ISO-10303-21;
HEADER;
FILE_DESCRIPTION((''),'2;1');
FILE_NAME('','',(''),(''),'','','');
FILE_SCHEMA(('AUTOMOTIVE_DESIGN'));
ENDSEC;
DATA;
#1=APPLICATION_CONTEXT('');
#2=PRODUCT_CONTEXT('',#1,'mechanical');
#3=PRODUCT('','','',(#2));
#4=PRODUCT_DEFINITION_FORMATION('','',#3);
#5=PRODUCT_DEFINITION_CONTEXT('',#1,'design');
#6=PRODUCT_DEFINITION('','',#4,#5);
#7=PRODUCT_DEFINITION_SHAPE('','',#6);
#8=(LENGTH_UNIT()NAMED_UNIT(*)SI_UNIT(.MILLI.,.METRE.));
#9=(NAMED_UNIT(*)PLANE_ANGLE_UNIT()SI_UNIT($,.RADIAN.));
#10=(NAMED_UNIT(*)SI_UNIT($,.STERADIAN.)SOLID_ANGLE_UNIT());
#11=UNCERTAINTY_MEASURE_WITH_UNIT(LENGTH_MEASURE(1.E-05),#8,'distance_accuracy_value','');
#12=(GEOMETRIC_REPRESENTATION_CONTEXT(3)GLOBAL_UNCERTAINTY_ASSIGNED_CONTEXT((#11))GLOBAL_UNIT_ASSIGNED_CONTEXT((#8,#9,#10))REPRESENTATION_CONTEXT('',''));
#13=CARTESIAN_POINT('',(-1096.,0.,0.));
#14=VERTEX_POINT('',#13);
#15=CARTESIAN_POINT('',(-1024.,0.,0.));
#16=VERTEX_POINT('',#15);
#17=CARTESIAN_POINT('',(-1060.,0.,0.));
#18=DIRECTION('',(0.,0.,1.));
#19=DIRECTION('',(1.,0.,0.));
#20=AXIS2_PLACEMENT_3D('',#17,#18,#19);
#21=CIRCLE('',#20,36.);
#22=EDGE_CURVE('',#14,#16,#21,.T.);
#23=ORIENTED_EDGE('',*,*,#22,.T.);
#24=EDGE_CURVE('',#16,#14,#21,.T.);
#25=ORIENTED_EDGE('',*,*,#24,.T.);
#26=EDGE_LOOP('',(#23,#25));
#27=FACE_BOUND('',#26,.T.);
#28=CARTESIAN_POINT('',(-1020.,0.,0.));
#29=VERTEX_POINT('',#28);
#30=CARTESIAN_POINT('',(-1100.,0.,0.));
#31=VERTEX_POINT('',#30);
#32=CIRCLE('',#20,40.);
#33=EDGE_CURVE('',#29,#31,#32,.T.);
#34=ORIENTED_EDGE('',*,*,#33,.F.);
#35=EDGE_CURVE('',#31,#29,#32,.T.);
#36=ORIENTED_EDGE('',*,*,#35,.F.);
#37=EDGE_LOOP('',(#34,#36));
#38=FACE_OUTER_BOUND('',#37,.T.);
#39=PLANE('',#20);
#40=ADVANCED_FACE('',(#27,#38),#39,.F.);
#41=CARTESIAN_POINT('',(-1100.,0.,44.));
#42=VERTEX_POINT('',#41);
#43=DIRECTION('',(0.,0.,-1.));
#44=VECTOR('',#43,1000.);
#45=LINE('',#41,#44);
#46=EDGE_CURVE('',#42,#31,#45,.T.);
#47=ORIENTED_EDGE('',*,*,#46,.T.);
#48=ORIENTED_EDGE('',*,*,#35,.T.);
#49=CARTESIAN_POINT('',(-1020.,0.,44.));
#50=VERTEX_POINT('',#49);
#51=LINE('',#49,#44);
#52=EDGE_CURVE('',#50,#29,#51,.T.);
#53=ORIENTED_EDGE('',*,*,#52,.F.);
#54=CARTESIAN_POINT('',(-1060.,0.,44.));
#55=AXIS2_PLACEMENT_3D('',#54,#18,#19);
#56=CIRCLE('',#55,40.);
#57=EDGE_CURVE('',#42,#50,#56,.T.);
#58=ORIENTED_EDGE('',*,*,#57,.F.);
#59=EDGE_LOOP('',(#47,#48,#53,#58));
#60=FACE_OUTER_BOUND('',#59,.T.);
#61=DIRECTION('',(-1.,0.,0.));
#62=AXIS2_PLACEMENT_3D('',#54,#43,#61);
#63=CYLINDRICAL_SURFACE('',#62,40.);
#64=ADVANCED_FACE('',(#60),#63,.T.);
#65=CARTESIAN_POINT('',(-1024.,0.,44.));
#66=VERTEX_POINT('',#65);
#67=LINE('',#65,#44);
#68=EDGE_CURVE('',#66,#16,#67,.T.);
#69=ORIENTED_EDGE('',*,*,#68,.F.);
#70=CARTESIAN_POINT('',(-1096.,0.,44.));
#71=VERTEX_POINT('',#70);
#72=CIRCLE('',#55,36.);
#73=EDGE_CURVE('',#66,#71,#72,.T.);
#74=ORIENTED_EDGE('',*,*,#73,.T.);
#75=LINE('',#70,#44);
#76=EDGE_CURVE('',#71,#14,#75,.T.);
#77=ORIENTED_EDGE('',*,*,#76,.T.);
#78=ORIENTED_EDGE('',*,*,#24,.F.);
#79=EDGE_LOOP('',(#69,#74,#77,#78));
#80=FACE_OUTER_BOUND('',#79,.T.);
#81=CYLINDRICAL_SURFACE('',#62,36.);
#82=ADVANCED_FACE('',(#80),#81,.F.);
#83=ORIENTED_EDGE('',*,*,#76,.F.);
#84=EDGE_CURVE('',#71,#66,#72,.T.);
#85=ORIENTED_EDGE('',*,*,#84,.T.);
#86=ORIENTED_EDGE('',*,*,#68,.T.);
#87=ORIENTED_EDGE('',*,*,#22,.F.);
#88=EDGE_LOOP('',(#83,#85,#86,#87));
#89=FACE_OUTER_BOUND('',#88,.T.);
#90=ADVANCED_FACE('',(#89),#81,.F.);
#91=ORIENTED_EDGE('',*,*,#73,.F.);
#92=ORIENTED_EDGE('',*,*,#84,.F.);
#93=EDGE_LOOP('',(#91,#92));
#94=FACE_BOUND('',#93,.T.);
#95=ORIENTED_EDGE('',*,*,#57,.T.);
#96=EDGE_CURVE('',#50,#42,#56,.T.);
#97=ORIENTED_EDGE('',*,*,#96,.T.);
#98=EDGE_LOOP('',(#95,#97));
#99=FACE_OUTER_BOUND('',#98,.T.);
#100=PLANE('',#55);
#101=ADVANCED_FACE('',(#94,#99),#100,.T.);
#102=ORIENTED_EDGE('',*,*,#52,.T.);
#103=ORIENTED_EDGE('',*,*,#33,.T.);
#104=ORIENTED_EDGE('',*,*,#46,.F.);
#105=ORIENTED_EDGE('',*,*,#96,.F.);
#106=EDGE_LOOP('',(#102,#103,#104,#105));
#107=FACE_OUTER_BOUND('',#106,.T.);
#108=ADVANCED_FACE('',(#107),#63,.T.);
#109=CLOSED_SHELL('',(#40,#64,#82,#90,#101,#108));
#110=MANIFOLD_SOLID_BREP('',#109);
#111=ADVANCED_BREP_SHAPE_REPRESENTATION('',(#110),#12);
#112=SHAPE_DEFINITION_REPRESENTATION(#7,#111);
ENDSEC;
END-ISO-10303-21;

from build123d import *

# Parameters (mm, degrees)
SKETCH1_R           = 40
SKETCH1_R_2         = 36
BOSS_EXTRUDE1_DEPTH = 44


with BuildPart() as part:
    # Sketch1 → Boss-Extrude1 (new body)
    with BuildSketch(Plane.XY):
        with Locations((-1060, 0)):
            Circle(SKETCH1_R)
        with Locations((-1060, 0)):
            Circle(SKETCH1_R_2, mode=Mode.SUBTRACT)
    extrude(amount=BOSS_EXTRUDE1_DEPTH)


solid = part.part
